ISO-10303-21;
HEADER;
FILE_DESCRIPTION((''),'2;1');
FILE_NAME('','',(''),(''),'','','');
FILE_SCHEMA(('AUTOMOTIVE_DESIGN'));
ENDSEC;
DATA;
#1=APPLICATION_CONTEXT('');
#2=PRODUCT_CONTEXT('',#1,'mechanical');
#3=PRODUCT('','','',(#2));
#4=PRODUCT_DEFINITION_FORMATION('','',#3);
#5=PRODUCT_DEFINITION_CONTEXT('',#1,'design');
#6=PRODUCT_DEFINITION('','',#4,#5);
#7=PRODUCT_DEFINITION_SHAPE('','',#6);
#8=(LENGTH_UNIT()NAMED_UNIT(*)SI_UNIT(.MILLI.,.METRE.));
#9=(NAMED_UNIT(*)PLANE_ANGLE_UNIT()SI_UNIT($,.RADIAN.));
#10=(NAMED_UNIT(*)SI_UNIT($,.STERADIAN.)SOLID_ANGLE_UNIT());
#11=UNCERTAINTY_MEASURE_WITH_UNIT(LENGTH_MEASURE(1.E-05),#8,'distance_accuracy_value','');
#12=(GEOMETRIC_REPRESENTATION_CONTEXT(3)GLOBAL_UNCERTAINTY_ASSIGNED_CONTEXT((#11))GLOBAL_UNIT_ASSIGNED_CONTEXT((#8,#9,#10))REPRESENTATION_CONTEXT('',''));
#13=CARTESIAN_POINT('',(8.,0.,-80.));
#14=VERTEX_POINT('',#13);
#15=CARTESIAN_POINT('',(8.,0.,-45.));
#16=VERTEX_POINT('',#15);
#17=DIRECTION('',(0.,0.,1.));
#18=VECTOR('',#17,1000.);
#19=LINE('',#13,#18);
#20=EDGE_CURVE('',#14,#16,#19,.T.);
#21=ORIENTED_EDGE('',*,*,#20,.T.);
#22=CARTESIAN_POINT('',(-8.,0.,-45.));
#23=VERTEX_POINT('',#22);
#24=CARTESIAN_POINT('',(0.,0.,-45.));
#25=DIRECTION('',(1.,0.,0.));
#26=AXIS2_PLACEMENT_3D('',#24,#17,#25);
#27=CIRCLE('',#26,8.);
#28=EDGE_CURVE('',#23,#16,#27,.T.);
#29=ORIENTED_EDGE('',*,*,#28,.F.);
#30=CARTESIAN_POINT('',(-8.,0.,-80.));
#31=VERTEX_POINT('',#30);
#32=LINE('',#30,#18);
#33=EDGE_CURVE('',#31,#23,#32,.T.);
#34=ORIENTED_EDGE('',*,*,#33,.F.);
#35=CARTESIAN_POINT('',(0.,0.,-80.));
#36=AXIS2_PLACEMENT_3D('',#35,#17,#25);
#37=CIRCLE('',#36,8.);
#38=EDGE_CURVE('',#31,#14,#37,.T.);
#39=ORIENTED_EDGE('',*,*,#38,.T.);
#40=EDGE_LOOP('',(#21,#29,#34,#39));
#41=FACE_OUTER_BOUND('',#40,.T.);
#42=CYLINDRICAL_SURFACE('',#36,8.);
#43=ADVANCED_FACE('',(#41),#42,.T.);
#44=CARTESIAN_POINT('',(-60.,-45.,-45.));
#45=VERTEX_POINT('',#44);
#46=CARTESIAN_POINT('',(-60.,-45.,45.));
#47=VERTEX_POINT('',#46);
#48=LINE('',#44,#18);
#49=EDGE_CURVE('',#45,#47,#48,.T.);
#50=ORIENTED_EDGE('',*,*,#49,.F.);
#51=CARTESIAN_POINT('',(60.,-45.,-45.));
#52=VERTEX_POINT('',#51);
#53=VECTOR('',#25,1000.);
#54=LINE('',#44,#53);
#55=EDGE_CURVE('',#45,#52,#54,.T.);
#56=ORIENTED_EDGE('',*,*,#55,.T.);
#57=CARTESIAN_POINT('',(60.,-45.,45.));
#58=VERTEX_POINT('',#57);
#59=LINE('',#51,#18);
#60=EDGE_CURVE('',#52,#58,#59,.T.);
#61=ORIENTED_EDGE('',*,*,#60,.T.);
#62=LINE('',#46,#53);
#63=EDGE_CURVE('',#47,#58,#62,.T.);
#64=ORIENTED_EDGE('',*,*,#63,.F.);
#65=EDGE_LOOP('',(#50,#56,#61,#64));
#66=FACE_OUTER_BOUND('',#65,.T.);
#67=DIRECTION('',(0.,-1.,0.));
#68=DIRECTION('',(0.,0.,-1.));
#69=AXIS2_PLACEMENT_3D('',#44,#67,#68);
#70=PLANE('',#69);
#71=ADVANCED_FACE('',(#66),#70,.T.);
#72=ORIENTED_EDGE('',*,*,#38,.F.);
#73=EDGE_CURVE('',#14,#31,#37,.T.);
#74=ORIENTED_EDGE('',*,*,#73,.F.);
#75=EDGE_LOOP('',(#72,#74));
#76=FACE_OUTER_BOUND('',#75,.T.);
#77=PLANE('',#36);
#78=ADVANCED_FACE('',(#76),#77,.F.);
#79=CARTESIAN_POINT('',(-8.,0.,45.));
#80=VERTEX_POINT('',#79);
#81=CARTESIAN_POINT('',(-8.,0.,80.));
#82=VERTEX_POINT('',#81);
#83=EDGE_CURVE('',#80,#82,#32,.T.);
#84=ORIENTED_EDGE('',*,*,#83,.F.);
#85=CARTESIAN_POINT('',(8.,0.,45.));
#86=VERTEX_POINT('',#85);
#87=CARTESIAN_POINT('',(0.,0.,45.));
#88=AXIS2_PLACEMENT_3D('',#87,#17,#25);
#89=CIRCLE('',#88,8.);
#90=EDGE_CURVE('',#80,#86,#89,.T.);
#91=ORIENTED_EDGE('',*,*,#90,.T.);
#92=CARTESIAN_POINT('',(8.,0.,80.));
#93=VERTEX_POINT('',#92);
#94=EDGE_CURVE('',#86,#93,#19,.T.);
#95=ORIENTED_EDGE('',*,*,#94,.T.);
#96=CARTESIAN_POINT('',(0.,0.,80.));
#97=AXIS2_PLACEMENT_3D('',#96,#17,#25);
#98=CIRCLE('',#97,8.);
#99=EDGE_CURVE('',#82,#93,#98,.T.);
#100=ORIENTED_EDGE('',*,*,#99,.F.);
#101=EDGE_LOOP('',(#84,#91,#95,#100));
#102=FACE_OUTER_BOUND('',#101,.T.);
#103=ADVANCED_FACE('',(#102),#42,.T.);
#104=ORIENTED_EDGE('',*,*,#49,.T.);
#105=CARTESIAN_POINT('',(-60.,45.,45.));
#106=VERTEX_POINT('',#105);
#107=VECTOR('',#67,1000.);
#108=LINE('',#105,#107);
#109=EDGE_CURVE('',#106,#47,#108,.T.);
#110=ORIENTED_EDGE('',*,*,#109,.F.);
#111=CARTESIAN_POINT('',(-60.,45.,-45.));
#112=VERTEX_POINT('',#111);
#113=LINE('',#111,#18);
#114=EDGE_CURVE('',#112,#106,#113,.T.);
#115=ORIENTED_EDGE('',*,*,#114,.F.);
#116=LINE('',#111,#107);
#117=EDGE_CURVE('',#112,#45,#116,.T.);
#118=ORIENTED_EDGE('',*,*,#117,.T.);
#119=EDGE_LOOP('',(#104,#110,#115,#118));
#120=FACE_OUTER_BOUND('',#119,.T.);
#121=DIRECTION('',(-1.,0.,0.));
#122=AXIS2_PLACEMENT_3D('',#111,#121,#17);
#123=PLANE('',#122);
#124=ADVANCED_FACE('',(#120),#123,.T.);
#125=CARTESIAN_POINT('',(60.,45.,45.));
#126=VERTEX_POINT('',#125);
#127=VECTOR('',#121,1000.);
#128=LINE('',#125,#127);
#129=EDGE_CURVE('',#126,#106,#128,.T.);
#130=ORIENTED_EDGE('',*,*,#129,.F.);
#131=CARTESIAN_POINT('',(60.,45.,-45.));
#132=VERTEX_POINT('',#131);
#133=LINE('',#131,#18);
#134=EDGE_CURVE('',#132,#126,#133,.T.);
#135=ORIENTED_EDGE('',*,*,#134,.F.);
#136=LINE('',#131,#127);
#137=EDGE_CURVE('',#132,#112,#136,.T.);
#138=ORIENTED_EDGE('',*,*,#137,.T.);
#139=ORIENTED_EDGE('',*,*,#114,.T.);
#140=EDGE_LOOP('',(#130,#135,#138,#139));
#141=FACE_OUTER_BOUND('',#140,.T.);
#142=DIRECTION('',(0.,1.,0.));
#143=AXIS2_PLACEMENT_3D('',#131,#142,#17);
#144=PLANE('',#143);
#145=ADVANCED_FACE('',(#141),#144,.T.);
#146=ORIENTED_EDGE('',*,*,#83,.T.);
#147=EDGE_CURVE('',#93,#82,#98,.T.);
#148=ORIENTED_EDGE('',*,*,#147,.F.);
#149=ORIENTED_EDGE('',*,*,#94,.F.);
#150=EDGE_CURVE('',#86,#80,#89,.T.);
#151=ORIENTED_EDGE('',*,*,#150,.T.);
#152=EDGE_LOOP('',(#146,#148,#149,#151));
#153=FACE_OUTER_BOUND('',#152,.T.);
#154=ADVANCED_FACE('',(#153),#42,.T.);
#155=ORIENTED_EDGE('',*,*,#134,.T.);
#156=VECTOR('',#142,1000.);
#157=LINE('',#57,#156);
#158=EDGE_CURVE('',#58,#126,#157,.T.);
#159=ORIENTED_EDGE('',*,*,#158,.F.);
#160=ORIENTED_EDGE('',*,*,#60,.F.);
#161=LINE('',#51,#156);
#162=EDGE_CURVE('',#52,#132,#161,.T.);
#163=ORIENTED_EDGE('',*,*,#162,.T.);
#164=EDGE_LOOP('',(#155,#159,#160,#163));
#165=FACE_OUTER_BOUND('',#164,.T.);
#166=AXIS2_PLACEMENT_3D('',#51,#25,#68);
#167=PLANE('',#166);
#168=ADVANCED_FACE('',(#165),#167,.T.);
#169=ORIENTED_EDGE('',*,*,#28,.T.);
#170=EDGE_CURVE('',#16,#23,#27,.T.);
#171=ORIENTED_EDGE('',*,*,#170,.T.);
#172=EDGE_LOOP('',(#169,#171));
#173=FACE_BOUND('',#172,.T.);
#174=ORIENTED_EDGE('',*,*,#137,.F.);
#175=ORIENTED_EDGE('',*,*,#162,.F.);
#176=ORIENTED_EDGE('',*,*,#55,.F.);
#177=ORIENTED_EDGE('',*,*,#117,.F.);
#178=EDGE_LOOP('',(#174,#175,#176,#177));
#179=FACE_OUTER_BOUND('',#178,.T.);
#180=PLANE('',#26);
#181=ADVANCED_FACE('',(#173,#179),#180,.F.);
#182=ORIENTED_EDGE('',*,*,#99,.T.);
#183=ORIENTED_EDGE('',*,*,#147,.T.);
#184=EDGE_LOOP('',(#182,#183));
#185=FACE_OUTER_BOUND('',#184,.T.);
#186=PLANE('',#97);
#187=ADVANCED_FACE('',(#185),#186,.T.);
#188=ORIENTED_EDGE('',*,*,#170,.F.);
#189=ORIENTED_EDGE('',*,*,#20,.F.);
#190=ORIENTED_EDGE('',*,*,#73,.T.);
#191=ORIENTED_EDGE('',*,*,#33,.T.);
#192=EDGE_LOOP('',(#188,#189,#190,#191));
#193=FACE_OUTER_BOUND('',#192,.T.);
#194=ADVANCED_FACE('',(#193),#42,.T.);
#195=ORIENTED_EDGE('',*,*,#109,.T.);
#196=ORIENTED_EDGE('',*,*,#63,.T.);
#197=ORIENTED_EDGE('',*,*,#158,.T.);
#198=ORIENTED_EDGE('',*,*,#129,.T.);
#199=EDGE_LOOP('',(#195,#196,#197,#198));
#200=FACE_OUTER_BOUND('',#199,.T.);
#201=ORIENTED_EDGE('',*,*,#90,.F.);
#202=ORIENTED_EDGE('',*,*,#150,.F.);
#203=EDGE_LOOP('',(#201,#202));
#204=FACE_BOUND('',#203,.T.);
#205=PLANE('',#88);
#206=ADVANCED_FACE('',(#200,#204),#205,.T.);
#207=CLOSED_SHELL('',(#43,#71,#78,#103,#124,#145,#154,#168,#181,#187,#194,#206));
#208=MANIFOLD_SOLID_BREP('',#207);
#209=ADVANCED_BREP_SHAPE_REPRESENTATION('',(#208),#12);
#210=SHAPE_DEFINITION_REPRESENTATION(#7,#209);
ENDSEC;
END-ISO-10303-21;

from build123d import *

# Parameters (mm, degrees)
SKETCH_1_W      = 120
SKETCH_1_H      = 90
EXTRUDE_1_DEPTH = 45
SKETCH_2_R      = 8
EXTRUDE_2_DEPTH = 80


with BuildPart() as part:
    # 草图1 → 凸台-拉伸1 (new, symmetric)
    with BuildSketch(Plane.XY):
        Rectangle(SKETCH_1_W, SKETCH_1_H)
    extrude(amount=EXTRUDE_1_DEPTH, both=True)

    # 草图2 → 凸台-拉伸2 (add, symmetric)
    with BuildSketch(Plane.XY):
        Circle(SKETCH_2_R)
    extrude(amount=EXTRUDE_2_DEPTH, both=True)


solid = part.part
